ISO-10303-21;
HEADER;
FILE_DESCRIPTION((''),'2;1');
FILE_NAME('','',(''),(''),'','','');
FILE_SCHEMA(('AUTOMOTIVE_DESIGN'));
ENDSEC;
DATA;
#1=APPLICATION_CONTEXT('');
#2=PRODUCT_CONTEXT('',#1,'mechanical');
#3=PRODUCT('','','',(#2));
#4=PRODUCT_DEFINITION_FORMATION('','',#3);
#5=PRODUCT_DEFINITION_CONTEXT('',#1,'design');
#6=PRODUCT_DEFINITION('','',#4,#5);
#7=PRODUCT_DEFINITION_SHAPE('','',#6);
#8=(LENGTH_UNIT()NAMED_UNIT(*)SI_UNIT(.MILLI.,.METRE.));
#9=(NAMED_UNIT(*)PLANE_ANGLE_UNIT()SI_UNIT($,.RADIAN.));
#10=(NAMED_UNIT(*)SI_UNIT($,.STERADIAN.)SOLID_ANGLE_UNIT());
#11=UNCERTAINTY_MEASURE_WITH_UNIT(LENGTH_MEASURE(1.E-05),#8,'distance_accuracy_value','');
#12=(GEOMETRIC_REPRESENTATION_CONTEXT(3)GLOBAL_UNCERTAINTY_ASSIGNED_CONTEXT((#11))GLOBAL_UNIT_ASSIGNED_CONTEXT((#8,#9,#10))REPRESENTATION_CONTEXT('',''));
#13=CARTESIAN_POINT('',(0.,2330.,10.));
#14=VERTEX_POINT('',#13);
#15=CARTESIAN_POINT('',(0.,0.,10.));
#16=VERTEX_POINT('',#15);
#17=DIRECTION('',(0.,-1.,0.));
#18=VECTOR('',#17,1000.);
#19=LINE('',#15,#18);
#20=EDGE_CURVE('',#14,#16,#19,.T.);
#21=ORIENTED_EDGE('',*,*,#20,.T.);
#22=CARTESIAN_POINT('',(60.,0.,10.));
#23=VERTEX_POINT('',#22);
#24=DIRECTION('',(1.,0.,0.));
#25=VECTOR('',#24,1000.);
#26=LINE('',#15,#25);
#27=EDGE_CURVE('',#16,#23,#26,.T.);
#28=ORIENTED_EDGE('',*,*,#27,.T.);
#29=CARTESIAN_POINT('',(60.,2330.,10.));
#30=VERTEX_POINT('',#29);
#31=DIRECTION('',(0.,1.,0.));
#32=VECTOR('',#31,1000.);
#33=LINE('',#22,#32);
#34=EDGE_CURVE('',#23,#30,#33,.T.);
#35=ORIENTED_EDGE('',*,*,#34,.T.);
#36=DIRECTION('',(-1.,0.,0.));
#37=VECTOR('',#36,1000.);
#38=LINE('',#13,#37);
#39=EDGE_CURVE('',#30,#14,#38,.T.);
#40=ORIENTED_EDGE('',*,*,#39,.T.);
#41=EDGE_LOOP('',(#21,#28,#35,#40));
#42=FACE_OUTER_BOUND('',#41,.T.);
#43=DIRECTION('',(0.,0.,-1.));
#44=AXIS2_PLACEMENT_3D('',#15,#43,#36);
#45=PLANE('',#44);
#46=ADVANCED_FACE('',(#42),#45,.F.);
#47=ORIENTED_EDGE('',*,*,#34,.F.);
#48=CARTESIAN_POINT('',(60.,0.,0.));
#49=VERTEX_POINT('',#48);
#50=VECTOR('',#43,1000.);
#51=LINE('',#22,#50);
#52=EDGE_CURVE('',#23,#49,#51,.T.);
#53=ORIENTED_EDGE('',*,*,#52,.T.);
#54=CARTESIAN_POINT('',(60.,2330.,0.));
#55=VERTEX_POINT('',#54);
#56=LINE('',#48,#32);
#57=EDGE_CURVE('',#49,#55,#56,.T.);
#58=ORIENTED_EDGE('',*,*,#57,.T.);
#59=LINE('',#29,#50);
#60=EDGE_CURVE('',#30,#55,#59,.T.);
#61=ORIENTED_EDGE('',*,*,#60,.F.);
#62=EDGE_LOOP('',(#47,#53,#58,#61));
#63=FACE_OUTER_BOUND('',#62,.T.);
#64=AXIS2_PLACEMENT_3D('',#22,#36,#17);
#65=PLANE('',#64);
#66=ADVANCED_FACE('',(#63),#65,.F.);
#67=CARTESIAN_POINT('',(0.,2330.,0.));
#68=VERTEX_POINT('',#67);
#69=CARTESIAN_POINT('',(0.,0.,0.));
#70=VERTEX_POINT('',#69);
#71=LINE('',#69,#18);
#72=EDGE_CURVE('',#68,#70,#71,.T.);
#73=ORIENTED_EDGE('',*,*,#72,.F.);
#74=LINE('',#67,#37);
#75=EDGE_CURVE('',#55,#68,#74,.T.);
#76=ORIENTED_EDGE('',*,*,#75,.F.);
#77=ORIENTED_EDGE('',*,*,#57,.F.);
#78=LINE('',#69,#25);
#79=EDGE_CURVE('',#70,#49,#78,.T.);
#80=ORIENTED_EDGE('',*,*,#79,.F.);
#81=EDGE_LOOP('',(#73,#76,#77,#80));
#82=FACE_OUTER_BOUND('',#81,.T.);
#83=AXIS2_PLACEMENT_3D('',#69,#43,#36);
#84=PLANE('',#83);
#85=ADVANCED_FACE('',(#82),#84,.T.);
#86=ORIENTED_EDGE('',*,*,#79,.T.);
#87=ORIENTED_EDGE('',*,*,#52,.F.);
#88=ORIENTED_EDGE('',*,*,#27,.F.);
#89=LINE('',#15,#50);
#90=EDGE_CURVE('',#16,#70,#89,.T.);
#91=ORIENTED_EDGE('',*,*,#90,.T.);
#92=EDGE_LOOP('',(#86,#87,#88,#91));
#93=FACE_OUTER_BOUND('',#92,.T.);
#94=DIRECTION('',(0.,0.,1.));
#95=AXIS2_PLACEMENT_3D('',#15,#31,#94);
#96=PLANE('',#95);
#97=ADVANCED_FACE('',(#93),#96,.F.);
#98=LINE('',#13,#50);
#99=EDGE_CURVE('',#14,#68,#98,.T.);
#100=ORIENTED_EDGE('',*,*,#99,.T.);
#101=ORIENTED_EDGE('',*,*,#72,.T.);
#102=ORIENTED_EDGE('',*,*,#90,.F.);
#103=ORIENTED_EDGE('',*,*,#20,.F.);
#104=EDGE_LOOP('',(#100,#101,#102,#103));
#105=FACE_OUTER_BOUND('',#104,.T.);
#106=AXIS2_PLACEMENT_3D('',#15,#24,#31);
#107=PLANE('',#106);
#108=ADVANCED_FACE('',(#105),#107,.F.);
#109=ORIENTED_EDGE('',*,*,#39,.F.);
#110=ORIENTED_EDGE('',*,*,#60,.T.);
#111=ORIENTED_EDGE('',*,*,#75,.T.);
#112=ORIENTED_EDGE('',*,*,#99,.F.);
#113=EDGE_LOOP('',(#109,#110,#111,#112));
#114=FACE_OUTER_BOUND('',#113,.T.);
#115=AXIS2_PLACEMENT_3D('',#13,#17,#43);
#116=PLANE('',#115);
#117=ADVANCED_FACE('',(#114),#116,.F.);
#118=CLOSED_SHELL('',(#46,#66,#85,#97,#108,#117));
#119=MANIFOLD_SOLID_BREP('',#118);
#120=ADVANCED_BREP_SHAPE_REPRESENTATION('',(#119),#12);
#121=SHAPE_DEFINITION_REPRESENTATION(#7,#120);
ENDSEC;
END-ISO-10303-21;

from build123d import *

# Parameters (mm, degrees)
SKETCH1_W           = 60
SKETCH1_H           = 2330
BOSS_EXTRUDE1_DEPTH = 10


with BuildPart() as part:
    # Sketch1 → Boss-Extrude1 (new body)
    with BuildSketch(Plane.XY):
        with Locations((30, 1165)):
            Rectangle(SKETCH1_W, SKETCH1_H)
    extrude(amount=BOSS_EXTRUDE1_DEPTH)


solid = part.part
